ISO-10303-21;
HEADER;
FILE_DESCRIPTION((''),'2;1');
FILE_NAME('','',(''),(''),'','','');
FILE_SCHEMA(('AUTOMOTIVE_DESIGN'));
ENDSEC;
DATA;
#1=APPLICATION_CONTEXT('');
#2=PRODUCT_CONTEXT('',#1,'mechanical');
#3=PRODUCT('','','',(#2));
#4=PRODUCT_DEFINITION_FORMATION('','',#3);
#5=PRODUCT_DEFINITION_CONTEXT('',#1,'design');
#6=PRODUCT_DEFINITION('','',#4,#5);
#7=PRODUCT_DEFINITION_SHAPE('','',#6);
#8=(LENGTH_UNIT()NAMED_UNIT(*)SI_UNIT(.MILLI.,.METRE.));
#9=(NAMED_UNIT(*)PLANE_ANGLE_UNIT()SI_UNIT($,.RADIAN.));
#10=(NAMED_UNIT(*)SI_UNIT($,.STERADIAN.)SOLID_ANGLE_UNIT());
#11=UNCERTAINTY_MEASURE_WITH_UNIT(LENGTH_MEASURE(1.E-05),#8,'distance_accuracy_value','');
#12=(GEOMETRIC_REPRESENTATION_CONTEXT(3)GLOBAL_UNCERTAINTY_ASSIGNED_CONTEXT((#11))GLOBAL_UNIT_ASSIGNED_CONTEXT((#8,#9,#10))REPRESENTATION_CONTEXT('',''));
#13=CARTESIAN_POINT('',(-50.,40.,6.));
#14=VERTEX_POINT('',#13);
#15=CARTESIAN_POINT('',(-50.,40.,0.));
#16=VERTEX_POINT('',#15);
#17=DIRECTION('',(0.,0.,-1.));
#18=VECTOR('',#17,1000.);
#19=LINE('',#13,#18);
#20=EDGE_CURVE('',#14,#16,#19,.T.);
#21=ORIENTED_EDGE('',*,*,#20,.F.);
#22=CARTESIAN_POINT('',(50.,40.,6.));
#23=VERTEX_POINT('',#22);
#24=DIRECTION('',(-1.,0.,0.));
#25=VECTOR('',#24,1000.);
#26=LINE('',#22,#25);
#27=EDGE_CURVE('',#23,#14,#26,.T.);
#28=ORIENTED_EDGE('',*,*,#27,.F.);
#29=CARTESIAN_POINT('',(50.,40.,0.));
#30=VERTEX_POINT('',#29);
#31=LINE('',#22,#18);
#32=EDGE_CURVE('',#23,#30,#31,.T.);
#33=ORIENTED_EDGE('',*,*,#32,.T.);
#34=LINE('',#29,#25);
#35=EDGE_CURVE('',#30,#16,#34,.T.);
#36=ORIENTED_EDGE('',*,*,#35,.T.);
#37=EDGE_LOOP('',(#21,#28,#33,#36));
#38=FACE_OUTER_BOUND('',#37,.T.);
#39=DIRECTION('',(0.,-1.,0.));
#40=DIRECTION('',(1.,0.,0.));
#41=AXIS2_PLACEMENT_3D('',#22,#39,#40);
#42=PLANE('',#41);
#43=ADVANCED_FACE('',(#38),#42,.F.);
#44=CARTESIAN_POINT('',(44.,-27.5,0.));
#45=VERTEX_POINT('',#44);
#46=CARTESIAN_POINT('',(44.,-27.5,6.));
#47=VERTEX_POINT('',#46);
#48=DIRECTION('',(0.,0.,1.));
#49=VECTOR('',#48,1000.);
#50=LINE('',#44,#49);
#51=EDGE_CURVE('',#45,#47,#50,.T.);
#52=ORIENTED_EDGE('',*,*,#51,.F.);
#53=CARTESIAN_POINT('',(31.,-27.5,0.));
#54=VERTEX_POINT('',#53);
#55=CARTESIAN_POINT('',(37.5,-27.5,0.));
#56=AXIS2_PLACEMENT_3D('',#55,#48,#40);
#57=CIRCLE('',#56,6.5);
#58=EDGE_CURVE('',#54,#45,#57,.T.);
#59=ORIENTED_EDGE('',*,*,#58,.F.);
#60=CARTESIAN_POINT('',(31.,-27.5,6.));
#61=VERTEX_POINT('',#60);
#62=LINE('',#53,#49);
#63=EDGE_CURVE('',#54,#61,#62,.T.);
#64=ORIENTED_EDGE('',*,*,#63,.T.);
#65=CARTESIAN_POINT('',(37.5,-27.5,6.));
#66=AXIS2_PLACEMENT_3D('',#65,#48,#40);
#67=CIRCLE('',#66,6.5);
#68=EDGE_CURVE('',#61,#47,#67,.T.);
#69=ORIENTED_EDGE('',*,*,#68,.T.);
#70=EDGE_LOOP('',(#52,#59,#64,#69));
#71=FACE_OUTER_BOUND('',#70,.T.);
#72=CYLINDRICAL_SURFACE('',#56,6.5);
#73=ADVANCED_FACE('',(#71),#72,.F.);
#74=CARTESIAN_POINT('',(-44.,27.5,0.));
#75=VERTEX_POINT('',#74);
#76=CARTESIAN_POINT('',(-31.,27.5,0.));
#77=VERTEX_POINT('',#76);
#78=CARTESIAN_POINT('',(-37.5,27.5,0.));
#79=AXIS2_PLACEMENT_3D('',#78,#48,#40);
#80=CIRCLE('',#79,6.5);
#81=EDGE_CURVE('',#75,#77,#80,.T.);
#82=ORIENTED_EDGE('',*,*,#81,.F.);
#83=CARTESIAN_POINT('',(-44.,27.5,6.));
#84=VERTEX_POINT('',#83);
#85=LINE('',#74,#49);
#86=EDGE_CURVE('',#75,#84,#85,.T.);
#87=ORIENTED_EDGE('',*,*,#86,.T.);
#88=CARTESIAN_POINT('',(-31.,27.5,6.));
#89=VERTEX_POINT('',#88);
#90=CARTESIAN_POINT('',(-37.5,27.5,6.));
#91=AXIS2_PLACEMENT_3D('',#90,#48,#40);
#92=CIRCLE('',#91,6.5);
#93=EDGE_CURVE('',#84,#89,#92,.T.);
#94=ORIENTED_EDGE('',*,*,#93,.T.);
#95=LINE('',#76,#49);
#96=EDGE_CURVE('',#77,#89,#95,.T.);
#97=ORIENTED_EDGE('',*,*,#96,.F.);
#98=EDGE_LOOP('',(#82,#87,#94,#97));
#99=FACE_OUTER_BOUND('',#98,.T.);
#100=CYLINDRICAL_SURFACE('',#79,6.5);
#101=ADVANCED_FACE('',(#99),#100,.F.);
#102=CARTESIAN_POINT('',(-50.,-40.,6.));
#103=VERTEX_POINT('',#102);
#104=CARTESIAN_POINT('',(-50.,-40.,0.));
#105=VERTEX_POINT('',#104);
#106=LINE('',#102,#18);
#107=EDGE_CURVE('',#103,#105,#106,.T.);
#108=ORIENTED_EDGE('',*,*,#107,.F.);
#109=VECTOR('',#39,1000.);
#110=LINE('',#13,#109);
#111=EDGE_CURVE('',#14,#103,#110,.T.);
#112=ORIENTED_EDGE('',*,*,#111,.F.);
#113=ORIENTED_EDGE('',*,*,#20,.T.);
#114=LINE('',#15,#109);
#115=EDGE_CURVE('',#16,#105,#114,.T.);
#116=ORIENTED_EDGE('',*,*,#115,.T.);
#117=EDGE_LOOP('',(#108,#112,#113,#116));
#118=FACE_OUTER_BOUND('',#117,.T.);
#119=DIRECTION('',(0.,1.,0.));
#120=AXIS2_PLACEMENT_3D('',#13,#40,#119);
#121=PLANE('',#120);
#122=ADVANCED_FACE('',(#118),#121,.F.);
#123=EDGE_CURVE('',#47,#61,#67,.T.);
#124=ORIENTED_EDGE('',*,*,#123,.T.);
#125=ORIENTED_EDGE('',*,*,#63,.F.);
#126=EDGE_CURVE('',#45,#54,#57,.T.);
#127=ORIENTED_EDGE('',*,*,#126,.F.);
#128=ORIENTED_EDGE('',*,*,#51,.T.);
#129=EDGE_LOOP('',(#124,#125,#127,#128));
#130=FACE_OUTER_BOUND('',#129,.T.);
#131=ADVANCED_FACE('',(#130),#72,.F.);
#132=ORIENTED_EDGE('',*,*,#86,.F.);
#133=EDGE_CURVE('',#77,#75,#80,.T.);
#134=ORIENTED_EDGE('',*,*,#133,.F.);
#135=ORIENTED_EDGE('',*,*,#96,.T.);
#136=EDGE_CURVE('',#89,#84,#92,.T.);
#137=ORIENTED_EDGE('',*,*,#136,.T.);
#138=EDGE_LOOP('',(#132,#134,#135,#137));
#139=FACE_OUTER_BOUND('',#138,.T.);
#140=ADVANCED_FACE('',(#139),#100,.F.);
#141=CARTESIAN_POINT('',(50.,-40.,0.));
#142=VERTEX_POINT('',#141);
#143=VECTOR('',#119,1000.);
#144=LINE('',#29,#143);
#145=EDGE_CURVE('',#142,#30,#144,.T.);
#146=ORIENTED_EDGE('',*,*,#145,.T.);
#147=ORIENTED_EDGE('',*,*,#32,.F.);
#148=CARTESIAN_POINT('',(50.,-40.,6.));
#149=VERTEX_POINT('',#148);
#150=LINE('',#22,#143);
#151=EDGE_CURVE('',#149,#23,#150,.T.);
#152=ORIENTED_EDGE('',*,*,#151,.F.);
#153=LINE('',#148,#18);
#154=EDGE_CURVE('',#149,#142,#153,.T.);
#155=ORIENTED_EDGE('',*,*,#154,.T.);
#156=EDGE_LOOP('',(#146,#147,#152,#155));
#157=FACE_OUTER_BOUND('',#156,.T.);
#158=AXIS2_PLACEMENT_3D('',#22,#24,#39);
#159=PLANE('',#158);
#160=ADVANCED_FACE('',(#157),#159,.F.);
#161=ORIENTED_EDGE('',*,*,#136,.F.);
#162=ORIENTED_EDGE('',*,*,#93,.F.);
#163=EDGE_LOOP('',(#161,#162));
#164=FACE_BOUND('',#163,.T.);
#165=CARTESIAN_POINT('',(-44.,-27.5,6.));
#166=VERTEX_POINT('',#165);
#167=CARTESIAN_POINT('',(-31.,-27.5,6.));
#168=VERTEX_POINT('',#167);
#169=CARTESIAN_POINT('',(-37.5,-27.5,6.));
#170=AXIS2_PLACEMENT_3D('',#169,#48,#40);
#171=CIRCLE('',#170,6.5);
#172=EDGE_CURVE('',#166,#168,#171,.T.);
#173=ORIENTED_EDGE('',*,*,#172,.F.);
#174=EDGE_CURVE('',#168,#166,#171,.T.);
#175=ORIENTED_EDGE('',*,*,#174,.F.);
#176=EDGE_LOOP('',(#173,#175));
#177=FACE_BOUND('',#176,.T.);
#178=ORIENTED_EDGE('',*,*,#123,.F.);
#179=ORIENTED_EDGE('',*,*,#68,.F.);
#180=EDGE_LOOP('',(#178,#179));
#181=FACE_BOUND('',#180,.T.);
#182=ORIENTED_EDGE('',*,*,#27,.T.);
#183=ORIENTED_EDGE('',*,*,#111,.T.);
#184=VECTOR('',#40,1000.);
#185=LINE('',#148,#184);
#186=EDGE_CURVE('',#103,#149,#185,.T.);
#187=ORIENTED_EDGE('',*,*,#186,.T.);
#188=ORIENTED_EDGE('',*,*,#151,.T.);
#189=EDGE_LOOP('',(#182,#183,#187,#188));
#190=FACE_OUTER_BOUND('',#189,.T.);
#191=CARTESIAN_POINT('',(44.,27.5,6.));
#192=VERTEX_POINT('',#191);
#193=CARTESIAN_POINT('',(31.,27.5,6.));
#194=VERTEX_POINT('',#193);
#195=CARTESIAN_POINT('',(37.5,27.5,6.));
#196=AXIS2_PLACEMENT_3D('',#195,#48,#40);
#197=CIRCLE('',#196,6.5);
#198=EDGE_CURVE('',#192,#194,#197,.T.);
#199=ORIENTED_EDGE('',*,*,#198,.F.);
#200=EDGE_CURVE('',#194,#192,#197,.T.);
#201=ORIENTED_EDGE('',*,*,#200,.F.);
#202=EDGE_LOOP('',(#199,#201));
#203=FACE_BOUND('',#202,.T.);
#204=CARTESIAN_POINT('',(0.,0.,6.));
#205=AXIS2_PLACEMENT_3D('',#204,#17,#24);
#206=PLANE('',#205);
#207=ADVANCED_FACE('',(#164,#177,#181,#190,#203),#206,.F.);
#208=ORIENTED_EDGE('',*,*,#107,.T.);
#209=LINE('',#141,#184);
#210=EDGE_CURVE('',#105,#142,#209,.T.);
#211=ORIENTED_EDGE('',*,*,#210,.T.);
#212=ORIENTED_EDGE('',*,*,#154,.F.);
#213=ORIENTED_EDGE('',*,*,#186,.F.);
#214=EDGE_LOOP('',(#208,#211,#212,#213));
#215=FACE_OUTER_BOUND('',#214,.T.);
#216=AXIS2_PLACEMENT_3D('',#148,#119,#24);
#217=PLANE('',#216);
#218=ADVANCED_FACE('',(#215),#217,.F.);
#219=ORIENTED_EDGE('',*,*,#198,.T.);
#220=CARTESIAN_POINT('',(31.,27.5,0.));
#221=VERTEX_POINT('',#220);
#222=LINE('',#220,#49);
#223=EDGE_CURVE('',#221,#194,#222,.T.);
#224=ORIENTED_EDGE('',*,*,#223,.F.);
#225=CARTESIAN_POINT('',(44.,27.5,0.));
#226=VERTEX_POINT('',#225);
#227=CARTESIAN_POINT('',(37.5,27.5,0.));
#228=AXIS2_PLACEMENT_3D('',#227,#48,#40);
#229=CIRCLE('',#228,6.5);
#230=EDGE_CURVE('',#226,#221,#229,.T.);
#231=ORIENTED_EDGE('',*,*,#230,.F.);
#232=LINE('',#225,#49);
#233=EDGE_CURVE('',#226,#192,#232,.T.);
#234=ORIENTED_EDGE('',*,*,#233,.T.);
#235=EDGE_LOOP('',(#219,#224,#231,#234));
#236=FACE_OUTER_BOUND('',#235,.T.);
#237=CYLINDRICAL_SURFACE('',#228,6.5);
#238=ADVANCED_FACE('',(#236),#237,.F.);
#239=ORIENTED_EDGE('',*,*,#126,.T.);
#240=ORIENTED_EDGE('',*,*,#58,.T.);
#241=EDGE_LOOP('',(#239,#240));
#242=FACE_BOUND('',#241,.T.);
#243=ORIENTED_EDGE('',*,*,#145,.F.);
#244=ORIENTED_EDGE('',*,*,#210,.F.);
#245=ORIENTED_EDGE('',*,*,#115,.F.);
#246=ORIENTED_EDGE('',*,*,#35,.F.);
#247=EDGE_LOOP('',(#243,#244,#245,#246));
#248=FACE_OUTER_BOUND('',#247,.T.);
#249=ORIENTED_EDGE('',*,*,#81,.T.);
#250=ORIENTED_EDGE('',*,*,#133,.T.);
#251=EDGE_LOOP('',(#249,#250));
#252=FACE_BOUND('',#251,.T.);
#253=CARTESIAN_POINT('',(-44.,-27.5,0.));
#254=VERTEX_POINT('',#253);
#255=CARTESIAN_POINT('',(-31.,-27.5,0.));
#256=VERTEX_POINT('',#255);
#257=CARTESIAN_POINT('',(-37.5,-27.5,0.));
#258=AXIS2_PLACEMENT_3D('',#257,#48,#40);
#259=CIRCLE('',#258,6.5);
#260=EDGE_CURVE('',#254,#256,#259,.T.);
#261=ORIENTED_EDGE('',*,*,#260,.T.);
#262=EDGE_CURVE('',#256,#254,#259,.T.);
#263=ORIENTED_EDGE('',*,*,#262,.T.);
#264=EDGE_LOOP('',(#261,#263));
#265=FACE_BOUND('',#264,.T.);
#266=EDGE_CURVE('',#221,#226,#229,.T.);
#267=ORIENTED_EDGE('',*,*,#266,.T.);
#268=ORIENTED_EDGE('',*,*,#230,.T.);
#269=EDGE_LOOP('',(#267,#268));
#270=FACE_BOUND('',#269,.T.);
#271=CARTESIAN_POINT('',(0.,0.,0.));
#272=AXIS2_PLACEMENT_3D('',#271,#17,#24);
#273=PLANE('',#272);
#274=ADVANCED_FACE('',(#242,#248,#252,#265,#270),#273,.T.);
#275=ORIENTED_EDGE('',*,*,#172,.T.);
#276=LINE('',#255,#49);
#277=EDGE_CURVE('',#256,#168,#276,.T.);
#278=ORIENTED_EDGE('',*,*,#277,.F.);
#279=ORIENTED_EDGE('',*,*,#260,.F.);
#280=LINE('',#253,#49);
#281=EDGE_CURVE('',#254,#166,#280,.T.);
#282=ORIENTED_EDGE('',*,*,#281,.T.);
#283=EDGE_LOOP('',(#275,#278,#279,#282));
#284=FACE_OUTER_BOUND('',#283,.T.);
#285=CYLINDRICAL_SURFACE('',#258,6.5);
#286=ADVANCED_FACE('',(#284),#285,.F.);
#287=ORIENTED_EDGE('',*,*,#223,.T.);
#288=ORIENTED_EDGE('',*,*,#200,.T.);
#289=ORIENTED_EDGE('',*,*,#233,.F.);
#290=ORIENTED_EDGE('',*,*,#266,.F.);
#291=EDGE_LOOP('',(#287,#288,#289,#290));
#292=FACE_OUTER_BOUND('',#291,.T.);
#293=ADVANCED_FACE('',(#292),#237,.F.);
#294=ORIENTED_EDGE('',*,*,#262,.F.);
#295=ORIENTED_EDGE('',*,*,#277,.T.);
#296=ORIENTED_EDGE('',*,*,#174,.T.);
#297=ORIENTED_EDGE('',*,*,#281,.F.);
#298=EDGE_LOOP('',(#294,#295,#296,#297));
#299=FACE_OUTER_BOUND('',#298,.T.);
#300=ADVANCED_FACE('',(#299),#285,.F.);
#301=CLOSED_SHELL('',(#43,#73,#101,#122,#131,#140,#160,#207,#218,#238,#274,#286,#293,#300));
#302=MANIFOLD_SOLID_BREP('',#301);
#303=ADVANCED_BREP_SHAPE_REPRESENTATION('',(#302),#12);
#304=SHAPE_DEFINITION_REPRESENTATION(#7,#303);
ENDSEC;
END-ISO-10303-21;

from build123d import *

# Parameters (mm, degrees)
SKETCH1_W           = 100
SKETCH1_H           = 80
BOSS_EXTRUDE1_DEPTH = 6
SKETCH2_R           = 6.5
CUT_EXTRUDE1_DEPTH  = 6


with BuildPart() as part:
    # Sketch1 → Boss-Extrude1 (new body)
    with BuildSketch(Plane.XY):
        Rectangle(SKETCH1_W, SKETCH1_H)
    extrude(amount=BOSS_EXTRUDE1_DEPTH)

    # Sketch2 → Cut-Extrude1 (cut)
    with BuildSketch(Plane.XY.offset(6)):
        with Locations((-37.5, 27.5)):
            Circle(SKETCH2_R)
        with Locations((37.5, 27.5)):
            Circle(SKETCH2_R)
        with Locations((37.5, -27.5)):
            Circle(SKETCH2_R)
        with Locations((-37.5, -27.5)):
            Circle(SKETCH2_R)
    extrude(amount=-CUT_EXTRUDE1_DEPTH, mode=Mode.SUBTRACT)


solid = part.part
